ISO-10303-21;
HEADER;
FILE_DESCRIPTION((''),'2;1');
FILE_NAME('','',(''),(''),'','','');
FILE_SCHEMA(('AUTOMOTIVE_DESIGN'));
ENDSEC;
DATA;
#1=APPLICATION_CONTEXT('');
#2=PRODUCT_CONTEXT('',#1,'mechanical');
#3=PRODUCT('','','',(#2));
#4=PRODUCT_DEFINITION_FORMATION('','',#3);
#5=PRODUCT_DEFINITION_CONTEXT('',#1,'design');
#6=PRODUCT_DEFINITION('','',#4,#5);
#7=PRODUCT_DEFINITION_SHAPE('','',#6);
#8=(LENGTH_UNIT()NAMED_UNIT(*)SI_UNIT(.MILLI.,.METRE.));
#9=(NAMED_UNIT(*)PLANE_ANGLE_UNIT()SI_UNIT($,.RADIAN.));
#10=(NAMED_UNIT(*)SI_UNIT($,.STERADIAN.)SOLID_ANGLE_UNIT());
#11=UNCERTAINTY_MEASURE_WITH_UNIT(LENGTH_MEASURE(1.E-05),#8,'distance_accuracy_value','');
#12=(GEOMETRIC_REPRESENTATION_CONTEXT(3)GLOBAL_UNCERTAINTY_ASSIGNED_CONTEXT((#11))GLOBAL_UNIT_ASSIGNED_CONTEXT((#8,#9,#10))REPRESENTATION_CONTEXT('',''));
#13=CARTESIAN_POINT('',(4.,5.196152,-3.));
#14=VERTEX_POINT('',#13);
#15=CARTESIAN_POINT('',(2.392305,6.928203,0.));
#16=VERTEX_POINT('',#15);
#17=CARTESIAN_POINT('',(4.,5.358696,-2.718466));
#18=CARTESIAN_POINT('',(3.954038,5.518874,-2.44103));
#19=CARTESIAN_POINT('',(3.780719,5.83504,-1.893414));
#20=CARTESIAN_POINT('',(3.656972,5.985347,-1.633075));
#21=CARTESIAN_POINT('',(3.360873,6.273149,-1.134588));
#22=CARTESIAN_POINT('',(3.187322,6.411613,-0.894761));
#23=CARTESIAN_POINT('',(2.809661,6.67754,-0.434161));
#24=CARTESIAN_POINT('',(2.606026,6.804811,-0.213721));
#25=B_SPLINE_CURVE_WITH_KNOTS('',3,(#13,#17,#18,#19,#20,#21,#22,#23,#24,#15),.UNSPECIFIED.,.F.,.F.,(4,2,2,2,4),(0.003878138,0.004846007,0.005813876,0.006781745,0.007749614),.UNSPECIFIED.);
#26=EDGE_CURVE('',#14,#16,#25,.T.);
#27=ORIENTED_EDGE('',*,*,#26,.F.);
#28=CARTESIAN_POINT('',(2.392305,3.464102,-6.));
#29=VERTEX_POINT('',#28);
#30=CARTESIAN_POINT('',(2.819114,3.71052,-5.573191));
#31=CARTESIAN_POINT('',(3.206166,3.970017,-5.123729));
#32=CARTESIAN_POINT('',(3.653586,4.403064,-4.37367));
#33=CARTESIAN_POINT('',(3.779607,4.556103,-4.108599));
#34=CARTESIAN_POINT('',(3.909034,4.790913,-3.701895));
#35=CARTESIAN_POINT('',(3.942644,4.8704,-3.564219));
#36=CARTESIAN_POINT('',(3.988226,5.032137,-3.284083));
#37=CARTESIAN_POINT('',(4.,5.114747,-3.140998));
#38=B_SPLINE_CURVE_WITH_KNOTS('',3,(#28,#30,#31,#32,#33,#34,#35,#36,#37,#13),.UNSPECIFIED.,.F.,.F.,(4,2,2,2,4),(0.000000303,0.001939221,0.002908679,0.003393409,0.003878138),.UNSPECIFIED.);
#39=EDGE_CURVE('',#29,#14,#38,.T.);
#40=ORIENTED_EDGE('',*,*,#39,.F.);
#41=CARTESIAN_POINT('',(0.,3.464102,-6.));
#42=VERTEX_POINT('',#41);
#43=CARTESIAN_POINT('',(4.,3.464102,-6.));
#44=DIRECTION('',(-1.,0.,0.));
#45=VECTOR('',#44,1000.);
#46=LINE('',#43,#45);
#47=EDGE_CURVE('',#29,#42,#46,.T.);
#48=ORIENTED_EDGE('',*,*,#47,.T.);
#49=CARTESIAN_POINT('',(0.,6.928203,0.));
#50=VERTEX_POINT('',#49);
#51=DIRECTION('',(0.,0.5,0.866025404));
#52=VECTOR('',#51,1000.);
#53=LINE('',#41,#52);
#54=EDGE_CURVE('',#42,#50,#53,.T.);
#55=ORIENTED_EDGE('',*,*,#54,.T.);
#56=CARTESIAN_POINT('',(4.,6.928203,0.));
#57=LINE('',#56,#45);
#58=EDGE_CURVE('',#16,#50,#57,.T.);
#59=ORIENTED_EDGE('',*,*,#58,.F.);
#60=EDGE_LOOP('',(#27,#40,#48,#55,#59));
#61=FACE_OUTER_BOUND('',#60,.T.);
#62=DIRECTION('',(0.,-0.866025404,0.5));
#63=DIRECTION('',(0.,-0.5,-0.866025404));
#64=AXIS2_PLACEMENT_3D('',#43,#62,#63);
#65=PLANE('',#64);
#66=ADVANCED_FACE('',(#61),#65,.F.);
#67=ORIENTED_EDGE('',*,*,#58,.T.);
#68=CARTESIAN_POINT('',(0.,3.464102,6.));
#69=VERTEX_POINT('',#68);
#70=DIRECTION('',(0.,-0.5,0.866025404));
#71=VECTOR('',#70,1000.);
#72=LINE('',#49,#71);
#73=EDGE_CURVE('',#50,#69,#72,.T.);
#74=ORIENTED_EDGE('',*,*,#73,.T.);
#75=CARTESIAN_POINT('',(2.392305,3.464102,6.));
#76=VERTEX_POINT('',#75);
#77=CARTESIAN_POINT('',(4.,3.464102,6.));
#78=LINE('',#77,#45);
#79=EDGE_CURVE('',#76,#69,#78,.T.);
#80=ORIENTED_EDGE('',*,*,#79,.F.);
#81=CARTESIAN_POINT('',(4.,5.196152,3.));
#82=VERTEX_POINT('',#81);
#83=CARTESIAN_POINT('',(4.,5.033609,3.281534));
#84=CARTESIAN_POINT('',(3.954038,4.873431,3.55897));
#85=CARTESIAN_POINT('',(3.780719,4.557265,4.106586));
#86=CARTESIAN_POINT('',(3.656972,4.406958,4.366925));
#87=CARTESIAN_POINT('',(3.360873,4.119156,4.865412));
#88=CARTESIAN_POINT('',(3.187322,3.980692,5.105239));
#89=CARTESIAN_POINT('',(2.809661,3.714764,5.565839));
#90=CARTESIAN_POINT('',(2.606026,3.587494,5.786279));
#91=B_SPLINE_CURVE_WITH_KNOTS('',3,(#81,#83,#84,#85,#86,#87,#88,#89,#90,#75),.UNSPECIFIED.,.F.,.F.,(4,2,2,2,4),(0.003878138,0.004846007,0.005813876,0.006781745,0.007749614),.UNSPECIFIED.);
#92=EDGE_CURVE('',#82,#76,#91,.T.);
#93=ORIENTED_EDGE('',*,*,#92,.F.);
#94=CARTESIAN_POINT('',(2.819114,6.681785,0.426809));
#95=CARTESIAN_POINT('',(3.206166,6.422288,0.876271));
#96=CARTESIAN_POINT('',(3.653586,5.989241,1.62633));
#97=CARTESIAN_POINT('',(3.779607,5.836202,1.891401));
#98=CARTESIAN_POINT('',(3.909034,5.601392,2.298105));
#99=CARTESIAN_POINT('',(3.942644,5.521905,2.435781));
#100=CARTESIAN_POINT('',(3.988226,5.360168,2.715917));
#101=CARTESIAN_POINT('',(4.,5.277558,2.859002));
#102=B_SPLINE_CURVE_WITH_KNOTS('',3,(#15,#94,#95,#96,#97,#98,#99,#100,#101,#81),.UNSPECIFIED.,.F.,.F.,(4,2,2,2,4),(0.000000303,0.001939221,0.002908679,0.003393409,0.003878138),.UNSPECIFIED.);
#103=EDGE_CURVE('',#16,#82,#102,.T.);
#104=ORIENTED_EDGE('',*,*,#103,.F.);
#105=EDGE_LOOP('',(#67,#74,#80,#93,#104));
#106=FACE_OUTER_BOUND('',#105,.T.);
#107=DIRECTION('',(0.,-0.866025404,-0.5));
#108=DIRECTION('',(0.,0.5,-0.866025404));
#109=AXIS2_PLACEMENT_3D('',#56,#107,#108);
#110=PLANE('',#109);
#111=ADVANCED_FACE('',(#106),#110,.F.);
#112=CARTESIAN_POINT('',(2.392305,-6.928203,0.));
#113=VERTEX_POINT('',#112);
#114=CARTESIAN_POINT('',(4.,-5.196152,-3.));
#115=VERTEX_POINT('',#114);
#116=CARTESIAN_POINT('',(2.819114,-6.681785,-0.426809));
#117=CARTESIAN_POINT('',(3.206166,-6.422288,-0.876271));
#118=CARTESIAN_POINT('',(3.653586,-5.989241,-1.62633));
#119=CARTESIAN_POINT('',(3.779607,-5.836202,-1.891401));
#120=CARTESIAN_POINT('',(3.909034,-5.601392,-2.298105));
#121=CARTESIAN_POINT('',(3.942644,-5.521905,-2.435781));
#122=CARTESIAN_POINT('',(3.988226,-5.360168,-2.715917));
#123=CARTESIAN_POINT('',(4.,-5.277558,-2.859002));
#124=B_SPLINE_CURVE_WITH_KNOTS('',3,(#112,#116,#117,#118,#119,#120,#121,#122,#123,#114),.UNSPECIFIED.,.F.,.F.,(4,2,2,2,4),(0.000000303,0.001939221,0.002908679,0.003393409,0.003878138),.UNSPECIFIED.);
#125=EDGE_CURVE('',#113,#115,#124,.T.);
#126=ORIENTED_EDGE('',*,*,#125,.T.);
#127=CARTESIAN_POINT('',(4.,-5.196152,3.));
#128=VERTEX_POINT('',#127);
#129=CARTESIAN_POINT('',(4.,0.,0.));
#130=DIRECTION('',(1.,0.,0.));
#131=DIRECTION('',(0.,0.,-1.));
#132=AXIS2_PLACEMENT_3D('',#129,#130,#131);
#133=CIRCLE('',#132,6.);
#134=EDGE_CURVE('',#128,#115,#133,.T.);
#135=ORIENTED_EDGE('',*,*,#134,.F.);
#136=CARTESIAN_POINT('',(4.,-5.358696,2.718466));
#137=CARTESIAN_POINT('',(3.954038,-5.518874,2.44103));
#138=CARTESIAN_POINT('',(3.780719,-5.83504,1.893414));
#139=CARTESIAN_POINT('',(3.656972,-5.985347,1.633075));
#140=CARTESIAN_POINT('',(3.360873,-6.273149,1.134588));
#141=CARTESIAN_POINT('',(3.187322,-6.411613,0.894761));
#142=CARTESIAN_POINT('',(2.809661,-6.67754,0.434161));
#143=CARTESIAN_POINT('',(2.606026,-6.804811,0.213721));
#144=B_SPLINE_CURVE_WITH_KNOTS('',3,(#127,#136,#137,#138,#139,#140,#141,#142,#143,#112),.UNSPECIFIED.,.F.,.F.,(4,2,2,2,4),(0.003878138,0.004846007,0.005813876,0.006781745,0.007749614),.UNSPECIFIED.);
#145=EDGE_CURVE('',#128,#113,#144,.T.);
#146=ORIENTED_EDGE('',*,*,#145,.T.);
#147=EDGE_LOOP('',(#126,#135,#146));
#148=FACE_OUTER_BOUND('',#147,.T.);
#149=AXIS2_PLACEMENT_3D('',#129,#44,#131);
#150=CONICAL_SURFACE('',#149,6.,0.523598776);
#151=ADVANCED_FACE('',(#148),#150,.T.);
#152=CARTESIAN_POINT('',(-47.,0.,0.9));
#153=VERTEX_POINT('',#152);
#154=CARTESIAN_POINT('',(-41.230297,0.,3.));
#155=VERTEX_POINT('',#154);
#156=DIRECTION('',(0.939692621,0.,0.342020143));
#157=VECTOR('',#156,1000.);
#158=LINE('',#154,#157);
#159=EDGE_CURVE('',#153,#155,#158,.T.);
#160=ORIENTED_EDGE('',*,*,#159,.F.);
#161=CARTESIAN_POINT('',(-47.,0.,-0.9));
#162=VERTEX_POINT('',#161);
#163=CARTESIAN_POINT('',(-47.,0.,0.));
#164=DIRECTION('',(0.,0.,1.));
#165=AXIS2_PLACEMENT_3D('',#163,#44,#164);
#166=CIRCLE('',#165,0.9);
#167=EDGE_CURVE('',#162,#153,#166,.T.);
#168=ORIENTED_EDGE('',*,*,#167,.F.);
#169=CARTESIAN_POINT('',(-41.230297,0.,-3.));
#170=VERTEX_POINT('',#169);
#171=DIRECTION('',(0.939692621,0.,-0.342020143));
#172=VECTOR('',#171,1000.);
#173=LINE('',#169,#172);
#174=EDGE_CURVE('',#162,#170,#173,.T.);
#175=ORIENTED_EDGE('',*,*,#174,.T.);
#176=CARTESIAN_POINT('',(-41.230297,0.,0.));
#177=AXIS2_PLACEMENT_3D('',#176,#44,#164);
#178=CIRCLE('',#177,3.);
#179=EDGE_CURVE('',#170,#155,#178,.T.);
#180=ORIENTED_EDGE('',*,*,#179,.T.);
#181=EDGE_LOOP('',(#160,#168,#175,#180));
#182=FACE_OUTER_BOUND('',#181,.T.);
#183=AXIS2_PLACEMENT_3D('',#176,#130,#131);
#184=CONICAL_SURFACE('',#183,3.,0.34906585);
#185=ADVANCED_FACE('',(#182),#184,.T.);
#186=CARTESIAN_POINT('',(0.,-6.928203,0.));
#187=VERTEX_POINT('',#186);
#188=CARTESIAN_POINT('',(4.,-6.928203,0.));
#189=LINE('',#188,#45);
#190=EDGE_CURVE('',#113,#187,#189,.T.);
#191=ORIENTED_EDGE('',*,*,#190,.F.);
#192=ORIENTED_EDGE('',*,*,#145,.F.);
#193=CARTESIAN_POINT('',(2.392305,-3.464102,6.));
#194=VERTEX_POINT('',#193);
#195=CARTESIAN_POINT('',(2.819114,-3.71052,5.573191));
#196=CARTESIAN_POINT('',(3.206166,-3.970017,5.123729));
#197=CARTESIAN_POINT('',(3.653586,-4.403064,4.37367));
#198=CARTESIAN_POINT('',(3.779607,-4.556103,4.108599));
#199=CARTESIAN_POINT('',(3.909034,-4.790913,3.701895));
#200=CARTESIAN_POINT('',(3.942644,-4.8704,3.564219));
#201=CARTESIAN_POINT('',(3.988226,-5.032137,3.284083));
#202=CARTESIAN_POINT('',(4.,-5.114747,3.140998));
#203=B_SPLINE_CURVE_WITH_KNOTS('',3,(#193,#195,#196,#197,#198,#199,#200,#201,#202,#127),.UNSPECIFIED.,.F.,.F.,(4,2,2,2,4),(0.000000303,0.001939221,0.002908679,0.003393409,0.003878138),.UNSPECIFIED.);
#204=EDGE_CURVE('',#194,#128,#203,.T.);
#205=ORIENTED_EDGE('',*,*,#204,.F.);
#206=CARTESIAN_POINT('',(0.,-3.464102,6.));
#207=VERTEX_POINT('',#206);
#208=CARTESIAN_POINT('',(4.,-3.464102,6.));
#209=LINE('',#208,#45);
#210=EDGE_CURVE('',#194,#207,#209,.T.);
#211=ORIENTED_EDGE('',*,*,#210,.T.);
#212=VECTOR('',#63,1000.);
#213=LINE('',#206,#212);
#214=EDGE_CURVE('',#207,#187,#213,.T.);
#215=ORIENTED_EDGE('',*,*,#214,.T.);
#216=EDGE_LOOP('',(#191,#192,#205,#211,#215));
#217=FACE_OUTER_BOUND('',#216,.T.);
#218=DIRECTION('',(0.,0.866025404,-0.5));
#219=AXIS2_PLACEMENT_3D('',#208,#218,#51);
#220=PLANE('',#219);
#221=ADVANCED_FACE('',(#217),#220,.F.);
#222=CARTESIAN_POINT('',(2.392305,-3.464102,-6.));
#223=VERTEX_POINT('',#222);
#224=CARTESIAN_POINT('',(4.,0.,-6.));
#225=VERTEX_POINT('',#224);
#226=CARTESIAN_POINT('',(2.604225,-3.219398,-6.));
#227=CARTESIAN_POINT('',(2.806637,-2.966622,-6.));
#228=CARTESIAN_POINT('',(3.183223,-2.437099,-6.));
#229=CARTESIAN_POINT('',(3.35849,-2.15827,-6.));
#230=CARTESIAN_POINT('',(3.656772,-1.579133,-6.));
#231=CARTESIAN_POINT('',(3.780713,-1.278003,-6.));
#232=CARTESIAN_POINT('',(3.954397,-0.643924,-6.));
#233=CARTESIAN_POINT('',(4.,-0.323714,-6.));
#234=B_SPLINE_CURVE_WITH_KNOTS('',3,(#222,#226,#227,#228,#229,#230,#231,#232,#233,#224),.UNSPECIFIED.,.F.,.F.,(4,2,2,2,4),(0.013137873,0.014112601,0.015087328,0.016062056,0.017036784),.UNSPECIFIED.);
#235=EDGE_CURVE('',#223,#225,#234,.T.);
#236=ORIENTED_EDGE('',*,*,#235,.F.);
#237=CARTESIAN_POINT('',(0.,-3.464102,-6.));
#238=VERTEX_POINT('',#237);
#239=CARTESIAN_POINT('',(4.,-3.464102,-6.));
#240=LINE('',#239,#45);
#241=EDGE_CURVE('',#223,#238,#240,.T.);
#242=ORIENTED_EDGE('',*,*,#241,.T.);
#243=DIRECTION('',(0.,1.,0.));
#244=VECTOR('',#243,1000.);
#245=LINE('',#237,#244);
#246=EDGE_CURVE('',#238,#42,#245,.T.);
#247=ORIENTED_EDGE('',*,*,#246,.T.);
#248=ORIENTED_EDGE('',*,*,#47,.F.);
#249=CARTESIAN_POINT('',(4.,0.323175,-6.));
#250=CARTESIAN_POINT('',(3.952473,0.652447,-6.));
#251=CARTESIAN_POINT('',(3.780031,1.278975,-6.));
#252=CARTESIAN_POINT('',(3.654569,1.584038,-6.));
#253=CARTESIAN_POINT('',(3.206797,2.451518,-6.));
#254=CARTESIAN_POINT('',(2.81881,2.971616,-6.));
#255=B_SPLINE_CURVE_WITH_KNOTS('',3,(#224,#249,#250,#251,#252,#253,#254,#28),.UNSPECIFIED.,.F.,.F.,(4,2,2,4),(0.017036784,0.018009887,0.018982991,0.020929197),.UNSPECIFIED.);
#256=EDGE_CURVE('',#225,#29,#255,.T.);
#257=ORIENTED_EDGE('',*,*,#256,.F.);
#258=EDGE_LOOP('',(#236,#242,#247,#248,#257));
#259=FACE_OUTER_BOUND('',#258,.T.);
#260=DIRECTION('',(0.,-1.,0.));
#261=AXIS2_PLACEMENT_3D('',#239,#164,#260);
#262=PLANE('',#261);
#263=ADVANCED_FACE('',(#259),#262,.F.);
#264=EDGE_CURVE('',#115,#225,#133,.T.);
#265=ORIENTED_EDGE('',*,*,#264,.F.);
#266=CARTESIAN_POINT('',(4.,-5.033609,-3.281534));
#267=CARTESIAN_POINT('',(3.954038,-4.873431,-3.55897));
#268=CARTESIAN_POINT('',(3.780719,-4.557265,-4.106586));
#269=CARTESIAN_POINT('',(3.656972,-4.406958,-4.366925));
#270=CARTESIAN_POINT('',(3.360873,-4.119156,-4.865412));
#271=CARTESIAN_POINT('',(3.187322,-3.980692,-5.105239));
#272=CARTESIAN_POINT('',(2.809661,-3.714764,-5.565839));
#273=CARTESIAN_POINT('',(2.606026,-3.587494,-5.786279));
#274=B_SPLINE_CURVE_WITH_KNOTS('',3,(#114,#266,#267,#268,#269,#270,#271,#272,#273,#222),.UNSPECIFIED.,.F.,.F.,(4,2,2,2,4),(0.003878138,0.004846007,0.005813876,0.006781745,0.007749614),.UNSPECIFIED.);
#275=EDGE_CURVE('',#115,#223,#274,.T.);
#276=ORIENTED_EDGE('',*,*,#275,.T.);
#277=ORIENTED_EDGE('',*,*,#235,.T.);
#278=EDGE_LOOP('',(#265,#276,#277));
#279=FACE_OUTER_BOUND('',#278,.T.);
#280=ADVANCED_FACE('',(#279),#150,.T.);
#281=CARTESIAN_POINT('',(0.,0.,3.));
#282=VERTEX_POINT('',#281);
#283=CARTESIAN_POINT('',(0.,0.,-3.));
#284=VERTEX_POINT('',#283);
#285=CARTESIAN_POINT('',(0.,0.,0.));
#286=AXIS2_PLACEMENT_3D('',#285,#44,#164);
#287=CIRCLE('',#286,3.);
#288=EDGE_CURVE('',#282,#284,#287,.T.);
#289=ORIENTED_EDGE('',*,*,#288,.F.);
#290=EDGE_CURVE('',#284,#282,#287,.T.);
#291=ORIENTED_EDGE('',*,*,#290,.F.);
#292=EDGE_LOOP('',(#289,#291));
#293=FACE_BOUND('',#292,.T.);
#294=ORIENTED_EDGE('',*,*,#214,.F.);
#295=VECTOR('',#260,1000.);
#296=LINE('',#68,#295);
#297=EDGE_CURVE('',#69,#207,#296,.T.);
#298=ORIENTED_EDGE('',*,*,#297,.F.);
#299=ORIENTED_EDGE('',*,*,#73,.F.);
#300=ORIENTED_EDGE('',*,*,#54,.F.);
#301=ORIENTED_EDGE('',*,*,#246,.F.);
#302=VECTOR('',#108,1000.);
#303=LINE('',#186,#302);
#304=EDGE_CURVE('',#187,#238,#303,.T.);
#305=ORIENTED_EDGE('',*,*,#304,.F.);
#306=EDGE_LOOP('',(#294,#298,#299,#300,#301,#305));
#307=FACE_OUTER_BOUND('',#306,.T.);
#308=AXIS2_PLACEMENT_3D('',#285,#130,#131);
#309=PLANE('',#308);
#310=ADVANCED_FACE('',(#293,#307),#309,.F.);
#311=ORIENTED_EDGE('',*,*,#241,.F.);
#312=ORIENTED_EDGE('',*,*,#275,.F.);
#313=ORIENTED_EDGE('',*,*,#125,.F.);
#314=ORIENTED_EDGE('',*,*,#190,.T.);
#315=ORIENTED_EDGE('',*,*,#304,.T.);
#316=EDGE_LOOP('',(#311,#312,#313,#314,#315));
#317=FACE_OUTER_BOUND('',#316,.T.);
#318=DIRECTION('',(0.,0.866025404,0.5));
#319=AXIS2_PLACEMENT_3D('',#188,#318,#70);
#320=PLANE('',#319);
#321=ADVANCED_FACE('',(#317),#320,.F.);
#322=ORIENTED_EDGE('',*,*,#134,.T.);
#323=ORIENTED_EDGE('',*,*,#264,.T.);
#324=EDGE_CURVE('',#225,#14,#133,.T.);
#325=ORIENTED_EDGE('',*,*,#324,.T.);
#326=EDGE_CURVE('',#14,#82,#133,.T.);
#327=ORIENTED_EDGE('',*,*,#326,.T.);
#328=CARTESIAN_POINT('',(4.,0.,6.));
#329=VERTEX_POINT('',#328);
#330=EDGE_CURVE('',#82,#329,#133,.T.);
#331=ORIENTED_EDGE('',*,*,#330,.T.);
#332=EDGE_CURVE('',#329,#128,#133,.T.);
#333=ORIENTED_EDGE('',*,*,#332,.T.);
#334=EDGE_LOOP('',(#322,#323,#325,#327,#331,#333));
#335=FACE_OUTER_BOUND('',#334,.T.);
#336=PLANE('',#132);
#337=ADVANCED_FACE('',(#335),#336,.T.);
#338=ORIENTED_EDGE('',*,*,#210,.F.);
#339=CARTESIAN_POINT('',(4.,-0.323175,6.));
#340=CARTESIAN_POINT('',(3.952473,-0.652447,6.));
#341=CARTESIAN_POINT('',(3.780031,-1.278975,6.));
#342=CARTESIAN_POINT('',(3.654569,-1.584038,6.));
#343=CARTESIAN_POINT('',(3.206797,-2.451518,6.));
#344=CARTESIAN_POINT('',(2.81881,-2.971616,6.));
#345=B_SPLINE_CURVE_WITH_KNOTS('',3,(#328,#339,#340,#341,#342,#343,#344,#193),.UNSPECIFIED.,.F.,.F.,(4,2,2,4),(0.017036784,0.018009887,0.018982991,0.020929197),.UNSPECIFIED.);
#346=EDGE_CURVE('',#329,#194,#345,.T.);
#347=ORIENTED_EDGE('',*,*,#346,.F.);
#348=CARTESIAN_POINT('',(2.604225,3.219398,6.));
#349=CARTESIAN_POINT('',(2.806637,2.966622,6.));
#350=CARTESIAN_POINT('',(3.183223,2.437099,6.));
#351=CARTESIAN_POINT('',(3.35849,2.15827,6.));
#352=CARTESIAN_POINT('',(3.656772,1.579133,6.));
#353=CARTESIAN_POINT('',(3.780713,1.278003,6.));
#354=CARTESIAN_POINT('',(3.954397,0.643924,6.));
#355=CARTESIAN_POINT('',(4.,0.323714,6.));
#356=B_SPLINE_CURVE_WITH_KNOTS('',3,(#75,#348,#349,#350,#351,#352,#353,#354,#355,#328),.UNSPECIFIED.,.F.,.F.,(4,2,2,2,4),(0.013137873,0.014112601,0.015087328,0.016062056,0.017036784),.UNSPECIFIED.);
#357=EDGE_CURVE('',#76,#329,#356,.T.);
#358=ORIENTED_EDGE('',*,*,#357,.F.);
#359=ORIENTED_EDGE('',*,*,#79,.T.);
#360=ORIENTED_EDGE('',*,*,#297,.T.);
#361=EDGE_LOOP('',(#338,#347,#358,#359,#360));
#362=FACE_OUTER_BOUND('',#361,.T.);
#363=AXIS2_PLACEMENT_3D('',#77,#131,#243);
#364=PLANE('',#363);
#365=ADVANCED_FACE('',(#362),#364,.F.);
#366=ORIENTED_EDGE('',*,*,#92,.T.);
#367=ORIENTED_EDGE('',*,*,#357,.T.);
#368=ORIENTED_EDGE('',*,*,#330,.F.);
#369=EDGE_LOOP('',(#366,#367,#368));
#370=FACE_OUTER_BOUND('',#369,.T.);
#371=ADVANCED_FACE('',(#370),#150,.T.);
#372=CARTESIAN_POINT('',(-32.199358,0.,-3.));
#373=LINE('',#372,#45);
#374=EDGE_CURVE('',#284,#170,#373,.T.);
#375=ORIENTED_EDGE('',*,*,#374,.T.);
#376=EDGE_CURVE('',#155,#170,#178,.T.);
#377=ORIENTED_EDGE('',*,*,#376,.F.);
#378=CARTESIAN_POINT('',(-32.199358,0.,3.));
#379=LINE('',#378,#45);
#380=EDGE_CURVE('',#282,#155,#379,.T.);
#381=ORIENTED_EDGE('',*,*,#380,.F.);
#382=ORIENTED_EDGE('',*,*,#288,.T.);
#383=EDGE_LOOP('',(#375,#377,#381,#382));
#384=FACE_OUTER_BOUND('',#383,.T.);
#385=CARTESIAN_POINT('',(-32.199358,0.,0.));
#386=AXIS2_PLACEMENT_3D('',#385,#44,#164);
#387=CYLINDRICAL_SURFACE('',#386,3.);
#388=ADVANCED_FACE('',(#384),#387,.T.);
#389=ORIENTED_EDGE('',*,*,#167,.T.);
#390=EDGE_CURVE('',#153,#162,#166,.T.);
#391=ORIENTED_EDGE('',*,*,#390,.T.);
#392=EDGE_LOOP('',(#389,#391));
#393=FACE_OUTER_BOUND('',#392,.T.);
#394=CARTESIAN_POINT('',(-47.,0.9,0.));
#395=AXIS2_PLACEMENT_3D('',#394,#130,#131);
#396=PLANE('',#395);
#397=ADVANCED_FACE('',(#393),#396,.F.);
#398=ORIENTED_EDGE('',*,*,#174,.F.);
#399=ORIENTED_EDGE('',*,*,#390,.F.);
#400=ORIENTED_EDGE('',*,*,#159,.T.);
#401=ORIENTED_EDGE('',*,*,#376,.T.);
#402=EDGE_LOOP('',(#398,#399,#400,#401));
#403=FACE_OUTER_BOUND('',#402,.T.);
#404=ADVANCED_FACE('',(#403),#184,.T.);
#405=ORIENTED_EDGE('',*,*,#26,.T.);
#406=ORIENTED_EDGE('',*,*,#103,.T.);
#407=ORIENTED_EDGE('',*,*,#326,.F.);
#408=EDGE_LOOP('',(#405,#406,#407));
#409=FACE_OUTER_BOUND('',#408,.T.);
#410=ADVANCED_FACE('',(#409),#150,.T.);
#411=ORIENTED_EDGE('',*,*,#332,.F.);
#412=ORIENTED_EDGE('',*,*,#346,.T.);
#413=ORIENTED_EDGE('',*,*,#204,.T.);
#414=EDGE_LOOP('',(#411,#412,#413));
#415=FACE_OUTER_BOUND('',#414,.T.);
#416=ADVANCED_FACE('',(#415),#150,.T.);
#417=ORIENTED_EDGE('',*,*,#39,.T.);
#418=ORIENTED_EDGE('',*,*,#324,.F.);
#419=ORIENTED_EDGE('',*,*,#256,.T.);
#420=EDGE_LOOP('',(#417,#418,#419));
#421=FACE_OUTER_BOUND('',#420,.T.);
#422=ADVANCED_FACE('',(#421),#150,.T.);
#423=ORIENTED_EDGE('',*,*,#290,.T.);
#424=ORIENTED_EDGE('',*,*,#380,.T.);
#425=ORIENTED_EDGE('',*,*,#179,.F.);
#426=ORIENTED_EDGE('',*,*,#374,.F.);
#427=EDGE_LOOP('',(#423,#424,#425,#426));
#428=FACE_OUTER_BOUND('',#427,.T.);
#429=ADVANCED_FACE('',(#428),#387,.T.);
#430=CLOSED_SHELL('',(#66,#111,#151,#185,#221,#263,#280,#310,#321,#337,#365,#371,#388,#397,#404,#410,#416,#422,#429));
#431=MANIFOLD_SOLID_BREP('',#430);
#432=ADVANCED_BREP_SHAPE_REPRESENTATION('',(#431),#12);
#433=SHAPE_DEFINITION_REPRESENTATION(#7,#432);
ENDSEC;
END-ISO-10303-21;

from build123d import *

# Parameters (mm, degrees)
BOSS_EXTRUDE1_DEPTH = 4
SKETCH2_OUTSIDE_W   = 40.846
SKETCH2_OUTSIDE_H   = 42.702
SKETCH2_OUTSIDE_R   = 6
CUT_EXTRUDE1_DEPTH  = 20
CUT_EXTRUDE1_DRAFT  = -30


with BuildPart() as part:
    # Sketch1 → Boss-Extrude1 (new body)
    with BuildSketch(Plane(origin=(0, 0, 0), x_dir=(0, 0, -1), z_dir=(1, 0, 0))):
        Polygon((0, -6.92820323), (6, -3.464101615), (6, 3.464101615), (0, 6.92820323), (-6, 3.464101615), (-6, -3.464101615), align=None)
    extrude(amount=BOSS_EXTRUDE1_DEPTH)


with BuildPart() as cut_extrude1_tool:
    # Sketch2 outside → Cut-Extrude1 (with draft: the straight prism first)
    with BuildSketch(Plane(origin=(4, 0, 0), x_dir=(0, 0, -1), z_dir=(1, 0, 0))):
        Rectangle(SKETCH2_OUTSIDE_W, SKETCH2_OUTSIDE_H)
        Circle(SKETCH2_OUTSIDE_R, mode=Mode.SUBTRACT)
    extrude(amount=-CUT_EXTRUDE1_DEPTH)
    # Cut-Extrude1: the draft: its side faces are tilted about the plane it starts from
    cut_extrude1_sides = [cut_extrude1_tool.faces().sort_by_distance(p)[0] for p in [
        (-6, -21.351, 0),
        (-6, 0, -20.423),
        (-6, 21.351, 0),
        (-6, 0, 20.423),
        (-6, 0, 6),
    ]]
    draft(cut_extrude1_sides, Plane(origin=(4, 0, 0), x_dir=(0, 0, -1), z_dir=(1, 0, 0)), CUT_EXTRUDE1_DRAFT)


with BuildPart() as part_1:
    add(part.part)

    # Cut-Extrude1: cut by cut_extrude1_tool
    add(cut_extrude1_tool.part, mode=Mode.SUBTRACT)

    # Sketch3 → Revolve1 (revolve)
    with BuildSketch(Plane.XY, mode=Mode.PRIVATE) as revolve1_sk:
        Polygon((0, 0), (0, 3), (-41.230297419, 3), (-47, 0.9), (-47, 0), align=None)
    revolve(revolve1_sk.sketch.rotate(Axis((-32.199358367, 0, 0), (1, 0, 0)), 90), axis=Axis((-32.199358367, 0, 0), (1, 0, 0)))


solid = part_1.part
